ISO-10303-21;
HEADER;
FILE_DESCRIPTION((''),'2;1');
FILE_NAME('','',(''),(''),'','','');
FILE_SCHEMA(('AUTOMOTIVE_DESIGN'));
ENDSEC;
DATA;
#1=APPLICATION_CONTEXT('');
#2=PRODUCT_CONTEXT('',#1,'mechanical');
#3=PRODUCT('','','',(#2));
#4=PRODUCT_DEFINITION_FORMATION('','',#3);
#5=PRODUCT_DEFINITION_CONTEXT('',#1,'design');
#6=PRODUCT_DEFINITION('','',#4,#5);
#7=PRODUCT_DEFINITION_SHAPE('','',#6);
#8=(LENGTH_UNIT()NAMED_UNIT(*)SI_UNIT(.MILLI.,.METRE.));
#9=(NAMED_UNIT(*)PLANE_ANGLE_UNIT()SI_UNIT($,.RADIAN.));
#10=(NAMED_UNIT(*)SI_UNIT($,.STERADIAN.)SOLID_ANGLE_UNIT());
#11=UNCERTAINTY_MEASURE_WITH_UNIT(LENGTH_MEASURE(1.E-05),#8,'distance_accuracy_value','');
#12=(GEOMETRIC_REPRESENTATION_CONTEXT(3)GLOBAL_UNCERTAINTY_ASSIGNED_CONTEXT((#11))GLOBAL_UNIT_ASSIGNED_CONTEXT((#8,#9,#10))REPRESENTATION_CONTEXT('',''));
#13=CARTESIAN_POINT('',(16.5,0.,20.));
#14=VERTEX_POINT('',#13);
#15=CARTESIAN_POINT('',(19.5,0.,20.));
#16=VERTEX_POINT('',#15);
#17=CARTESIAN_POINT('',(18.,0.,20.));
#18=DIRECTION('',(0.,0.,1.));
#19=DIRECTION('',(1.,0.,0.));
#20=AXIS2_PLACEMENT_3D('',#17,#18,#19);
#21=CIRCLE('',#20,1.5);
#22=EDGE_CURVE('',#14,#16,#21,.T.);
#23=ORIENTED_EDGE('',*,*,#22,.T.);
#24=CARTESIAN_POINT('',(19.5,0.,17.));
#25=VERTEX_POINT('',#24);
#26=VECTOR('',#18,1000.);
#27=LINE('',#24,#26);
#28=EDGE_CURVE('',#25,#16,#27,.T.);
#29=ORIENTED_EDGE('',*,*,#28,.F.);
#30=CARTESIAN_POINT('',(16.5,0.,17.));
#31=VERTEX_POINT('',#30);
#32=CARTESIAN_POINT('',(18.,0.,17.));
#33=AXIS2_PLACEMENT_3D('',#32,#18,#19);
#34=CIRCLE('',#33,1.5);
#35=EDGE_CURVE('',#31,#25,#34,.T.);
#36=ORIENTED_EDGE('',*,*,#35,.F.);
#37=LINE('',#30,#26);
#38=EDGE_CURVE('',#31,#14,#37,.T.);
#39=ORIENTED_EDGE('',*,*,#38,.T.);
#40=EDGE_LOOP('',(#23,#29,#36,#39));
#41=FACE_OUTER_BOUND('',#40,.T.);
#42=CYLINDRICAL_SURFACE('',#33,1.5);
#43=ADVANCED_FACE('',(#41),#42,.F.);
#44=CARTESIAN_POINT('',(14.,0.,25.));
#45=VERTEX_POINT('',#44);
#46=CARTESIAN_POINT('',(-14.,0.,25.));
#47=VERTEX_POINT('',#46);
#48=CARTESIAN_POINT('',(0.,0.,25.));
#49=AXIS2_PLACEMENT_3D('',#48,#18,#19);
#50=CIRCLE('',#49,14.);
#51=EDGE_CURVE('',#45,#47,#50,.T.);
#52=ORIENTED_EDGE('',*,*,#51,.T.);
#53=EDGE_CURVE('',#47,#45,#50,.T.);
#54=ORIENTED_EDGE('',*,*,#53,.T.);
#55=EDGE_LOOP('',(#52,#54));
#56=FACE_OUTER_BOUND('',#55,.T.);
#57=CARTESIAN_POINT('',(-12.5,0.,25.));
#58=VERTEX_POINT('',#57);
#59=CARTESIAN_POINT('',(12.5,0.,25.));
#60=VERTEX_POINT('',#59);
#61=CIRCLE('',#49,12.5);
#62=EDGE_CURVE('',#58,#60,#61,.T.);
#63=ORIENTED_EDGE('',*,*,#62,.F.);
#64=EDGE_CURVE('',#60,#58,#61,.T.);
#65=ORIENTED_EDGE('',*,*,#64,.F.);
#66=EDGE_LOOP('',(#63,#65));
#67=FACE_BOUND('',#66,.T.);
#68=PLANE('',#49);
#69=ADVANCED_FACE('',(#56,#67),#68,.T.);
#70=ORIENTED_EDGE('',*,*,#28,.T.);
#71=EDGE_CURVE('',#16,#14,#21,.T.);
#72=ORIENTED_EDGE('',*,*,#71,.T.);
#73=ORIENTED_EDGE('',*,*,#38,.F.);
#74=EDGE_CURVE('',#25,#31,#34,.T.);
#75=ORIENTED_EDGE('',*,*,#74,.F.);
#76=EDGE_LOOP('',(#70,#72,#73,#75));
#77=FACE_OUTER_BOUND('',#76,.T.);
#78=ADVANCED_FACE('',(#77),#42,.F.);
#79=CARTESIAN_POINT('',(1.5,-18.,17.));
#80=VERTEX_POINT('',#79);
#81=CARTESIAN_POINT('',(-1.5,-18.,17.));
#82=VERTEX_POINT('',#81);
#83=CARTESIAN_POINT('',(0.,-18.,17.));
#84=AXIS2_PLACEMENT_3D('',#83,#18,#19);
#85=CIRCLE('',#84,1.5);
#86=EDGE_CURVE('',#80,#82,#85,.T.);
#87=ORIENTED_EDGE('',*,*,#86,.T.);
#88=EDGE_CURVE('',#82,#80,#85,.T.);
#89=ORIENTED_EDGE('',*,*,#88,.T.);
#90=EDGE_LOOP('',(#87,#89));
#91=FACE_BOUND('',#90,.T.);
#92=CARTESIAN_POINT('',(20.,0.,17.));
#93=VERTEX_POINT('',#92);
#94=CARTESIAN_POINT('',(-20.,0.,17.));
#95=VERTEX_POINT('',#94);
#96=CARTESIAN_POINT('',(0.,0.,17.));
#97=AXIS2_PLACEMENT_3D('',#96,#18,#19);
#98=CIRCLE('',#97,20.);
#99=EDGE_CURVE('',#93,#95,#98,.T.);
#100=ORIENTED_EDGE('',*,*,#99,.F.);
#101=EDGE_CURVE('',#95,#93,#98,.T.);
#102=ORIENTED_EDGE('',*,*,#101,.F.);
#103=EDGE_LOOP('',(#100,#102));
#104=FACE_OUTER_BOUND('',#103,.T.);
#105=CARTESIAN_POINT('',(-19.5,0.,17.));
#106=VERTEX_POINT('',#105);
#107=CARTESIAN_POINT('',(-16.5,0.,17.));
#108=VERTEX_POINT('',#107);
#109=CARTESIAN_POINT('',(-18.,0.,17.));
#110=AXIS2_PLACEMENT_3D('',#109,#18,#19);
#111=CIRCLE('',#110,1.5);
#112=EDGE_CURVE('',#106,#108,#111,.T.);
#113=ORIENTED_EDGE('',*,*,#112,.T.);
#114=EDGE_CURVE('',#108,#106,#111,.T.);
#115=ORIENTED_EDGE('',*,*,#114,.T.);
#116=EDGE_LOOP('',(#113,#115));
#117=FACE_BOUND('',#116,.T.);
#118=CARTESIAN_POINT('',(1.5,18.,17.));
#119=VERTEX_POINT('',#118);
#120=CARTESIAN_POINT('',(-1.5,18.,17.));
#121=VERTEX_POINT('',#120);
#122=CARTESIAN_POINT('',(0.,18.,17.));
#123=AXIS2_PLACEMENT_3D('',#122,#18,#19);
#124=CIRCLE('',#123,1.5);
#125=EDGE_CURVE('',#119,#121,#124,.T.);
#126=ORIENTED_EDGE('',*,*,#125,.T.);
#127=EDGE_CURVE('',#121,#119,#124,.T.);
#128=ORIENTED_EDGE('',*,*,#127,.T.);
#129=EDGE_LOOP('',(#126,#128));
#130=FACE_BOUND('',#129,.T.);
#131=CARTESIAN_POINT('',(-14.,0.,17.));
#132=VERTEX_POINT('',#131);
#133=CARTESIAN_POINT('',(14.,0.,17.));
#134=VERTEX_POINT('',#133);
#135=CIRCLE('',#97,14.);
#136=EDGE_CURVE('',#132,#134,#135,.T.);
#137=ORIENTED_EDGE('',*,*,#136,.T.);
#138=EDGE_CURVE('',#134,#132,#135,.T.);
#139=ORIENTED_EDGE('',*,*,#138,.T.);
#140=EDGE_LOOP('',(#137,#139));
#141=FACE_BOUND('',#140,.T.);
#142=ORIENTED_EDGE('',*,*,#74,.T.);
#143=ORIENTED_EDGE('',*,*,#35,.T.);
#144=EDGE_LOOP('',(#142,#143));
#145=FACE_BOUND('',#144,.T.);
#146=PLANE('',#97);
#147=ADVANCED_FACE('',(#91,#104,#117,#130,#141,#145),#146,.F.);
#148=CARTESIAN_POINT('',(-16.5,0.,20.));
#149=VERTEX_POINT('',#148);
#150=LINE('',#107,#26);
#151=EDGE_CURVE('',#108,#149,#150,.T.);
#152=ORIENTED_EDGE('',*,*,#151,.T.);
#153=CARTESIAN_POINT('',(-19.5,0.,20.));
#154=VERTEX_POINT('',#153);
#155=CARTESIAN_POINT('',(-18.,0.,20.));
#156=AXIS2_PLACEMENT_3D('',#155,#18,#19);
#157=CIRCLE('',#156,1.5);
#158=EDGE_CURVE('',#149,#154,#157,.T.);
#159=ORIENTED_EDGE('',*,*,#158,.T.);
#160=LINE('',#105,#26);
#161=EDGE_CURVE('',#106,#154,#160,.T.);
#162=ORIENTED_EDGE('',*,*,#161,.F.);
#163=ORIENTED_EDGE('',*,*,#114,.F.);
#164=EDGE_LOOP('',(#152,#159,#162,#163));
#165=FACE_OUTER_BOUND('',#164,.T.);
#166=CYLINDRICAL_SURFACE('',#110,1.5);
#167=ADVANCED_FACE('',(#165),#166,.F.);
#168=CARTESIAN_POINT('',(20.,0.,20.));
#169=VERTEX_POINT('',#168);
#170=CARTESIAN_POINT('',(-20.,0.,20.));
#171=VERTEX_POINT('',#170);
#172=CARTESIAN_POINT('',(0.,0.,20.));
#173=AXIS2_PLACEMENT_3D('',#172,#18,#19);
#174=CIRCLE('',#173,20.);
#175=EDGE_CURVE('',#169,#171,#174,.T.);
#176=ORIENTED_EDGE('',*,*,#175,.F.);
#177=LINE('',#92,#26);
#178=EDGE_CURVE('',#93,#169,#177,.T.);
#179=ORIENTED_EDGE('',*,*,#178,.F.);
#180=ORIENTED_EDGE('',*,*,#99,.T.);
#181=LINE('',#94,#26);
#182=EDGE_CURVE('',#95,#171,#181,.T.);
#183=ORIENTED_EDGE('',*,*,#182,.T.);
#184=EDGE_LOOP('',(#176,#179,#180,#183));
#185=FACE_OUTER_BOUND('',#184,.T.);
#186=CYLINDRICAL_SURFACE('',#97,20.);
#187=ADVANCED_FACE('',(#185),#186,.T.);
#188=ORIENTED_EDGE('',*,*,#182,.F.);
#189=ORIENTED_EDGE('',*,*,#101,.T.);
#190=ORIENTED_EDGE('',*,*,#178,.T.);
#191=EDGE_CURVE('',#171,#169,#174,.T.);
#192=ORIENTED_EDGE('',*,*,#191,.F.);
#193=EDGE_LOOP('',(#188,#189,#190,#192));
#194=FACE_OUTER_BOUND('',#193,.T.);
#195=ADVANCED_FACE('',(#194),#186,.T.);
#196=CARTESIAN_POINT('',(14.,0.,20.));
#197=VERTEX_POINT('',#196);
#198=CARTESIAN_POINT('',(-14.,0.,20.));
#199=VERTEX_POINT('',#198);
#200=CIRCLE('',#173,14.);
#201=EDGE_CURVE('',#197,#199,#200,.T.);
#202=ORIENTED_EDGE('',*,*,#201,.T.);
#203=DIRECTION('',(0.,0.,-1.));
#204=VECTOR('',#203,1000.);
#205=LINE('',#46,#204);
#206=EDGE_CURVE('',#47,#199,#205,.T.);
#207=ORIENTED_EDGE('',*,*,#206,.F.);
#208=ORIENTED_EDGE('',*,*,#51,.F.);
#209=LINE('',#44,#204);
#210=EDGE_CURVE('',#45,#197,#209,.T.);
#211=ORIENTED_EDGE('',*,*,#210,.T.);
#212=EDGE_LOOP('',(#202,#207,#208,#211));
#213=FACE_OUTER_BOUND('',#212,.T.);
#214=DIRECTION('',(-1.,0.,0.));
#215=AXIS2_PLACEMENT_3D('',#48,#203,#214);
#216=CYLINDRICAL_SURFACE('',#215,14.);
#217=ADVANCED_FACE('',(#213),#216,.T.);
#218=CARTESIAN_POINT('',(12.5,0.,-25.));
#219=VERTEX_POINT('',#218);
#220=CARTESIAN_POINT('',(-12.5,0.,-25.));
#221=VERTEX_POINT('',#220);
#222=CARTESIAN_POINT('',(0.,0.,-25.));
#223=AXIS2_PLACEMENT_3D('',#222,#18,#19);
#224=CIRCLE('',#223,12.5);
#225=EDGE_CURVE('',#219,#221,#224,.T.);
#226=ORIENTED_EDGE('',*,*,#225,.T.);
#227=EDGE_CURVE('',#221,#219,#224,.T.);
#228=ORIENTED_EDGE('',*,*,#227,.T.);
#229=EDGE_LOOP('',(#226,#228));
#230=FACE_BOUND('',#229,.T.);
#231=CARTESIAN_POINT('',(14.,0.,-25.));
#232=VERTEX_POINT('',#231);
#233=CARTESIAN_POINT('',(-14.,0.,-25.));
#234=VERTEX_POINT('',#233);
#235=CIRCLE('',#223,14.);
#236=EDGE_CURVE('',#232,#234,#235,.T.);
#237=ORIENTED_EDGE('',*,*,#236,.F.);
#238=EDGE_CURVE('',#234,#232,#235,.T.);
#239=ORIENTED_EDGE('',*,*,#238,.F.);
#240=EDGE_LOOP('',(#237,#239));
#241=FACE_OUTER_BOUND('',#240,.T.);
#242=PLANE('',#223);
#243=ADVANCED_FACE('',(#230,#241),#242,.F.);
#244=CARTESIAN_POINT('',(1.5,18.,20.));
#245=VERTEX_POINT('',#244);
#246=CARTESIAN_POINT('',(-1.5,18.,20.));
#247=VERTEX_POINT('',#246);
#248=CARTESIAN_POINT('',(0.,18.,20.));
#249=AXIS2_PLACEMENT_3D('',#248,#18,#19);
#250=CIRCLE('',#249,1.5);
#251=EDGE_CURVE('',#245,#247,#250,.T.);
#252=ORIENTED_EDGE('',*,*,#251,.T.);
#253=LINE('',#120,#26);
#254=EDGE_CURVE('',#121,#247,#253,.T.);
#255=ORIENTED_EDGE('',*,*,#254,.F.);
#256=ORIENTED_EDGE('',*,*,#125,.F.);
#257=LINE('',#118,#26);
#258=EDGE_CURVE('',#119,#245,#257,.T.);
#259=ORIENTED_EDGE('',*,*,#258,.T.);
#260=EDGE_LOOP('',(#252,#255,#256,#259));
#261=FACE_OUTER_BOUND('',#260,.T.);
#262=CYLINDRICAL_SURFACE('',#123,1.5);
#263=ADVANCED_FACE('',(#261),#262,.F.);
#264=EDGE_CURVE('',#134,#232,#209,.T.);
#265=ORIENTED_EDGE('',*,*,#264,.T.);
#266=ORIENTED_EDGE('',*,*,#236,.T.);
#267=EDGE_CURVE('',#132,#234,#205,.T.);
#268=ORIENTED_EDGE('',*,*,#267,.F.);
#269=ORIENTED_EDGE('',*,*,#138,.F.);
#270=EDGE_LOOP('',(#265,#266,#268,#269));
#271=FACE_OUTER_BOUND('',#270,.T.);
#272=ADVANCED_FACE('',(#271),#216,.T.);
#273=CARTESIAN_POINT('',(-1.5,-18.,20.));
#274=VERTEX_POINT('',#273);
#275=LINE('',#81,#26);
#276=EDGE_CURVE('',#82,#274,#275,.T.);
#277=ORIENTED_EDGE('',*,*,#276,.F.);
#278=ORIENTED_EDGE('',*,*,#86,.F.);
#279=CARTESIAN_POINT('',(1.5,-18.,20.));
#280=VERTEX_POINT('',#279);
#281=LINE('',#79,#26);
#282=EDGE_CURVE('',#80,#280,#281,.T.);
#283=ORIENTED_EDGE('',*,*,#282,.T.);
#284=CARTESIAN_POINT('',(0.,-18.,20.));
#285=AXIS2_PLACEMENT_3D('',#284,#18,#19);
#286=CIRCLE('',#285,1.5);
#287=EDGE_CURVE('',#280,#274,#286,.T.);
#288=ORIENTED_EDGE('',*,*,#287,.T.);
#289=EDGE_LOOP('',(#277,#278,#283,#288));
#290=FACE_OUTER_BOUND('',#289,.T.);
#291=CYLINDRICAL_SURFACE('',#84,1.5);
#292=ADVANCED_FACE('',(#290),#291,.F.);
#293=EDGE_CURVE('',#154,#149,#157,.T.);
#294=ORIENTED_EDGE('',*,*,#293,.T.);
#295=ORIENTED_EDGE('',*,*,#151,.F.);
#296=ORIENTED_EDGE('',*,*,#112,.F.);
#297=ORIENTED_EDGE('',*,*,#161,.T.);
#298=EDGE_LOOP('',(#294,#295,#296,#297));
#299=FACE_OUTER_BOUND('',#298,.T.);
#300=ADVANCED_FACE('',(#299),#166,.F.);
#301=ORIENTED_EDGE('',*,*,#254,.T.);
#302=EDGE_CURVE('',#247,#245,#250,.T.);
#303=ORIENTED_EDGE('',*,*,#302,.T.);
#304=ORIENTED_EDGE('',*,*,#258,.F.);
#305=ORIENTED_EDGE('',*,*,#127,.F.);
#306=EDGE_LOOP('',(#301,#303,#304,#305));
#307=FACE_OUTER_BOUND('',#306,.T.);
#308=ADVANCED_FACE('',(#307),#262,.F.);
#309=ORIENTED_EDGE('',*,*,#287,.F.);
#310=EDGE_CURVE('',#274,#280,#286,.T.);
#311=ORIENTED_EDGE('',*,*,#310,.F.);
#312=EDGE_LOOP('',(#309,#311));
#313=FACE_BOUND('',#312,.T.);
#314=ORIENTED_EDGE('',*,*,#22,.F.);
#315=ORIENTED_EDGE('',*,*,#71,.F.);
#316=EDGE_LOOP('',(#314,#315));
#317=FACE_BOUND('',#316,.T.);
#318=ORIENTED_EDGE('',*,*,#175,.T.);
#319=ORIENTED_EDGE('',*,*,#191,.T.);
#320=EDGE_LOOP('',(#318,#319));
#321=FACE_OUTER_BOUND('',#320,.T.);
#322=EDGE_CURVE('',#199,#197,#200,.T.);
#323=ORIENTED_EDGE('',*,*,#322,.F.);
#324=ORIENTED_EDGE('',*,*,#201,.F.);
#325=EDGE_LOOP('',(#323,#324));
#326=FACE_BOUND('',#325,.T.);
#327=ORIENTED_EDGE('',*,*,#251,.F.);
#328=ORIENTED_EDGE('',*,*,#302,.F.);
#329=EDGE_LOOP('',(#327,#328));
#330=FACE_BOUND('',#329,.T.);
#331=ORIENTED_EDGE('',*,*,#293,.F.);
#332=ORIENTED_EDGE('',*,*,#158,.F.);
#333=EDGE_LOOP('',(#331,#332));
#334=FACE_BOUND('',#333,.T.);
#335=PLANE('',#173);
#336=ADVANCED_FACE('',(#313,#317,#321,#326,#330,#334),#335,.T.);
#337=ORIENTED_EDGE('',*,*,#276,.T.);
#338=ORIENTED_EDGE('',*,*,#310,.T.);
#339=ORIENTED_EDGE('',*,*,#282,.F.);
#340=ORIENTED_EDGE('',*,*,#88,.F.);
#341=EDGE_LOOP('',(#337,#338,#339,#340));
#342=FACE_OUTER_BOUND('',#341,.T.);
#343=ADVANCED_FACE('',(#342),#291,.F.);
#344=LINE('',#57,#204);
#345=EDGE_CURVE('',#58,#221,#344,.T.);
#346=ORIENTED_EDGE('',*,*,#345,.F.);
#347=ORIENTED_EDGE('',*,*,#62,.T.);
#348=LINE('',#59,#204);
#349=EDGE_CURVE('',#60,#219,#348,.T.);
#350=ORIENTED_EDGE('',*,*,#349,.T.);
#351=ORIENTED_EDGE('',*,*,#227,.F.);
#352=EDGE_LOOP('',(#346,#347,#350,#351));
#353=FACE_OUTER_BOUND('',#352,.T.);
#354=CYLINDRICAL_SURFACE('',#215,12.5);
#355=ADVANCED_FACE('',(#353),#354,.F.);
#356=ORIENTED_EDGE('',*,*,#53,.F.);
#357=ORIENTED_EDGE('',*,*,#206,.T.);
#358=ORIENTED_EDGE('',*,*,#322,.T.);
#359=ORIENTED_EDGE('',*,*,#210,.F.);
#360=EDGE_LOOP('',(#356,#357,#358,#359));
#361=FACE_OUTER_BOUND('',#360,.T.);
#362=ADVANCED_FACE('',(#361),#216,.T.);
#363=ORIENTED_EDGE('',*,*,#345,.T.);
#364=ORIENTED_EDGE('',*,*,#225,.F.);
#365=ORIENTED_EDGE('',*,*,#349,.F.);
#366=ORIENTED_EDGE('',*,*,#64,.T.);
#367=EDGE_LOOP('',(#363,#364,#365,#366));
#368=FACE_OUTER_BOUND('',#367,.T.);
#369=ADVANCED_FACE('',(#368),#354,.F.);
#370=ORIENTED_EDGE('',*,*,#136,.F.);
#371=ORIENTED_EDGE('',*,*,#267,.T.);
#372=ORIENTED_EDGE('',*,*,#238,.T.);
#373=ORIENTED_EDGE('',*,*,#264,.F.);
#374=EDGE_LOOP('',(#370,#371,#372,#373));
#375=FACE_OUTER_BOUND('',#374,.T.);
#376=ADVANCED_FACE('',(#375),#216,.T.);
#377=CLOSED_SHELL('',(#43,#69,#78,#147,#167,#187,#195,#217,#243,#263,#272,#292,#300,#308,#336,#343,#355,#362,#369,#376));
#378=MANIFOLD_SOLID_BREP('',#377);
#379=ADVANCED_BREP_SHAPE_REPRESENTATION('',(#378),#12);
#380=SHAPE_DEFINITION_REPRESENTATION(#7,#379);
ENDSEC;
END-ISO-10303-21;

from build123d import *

# Parameters (mm, degrees)
SKETCH1_R           = 14
SKETCH1_R_2         = 12.5
BOSS_EXTRUDE1_DEPTH = 25
BOSS_EXTRUDE2_START = -8
SKETCH2_R           = 20
SKETCH2_R_2         = 1.5
SKETCH2_R_3         = 12.5
BOSS_EXTRUDE2_DEPTH = 3


with BuildPart() as part:
    # Sketch1 → Boss-Extrude1 (new, symmetric)
    with BuildSketch(Plane.XY):
        Circle(SKETCH1_R)
        Circle(SKETCH1_R_2, mode=Mode.SUBTRACT)
    extrude(amount=BOSS_EXTRUDE1_DEPTH, both=True)

    # Sketch2 → Boss-Extrude2 (add)
    with BuildSketch(Plane.XY.offset(25).offset(BOSS_EXTRUDE2_START)):
        Circle(SKETCH2_R)
        with Locations((0, 18)):
            Circle(SKETCH2_R_2, mode=Mode.SUBTRACT)
        with Locations((18, 0)):
            Circle(SKETCH2_R_2, mode=Mode.SUBTRACT)
        with Locations((0, -18)):
            Circle(SKETCH2_R_2, mode=Mode.SUBTRACT)
        with Locations((-18, 0)):
            Circle(SKETCH2_R_2, mode=Mode.SUBTRACT)
        Circle(SKETCH2_R_3, mode=Mode.SUBTRACT)
    extrude(amount=BOSS_EXTRUDE2_DEPTH)


solid = part.part
